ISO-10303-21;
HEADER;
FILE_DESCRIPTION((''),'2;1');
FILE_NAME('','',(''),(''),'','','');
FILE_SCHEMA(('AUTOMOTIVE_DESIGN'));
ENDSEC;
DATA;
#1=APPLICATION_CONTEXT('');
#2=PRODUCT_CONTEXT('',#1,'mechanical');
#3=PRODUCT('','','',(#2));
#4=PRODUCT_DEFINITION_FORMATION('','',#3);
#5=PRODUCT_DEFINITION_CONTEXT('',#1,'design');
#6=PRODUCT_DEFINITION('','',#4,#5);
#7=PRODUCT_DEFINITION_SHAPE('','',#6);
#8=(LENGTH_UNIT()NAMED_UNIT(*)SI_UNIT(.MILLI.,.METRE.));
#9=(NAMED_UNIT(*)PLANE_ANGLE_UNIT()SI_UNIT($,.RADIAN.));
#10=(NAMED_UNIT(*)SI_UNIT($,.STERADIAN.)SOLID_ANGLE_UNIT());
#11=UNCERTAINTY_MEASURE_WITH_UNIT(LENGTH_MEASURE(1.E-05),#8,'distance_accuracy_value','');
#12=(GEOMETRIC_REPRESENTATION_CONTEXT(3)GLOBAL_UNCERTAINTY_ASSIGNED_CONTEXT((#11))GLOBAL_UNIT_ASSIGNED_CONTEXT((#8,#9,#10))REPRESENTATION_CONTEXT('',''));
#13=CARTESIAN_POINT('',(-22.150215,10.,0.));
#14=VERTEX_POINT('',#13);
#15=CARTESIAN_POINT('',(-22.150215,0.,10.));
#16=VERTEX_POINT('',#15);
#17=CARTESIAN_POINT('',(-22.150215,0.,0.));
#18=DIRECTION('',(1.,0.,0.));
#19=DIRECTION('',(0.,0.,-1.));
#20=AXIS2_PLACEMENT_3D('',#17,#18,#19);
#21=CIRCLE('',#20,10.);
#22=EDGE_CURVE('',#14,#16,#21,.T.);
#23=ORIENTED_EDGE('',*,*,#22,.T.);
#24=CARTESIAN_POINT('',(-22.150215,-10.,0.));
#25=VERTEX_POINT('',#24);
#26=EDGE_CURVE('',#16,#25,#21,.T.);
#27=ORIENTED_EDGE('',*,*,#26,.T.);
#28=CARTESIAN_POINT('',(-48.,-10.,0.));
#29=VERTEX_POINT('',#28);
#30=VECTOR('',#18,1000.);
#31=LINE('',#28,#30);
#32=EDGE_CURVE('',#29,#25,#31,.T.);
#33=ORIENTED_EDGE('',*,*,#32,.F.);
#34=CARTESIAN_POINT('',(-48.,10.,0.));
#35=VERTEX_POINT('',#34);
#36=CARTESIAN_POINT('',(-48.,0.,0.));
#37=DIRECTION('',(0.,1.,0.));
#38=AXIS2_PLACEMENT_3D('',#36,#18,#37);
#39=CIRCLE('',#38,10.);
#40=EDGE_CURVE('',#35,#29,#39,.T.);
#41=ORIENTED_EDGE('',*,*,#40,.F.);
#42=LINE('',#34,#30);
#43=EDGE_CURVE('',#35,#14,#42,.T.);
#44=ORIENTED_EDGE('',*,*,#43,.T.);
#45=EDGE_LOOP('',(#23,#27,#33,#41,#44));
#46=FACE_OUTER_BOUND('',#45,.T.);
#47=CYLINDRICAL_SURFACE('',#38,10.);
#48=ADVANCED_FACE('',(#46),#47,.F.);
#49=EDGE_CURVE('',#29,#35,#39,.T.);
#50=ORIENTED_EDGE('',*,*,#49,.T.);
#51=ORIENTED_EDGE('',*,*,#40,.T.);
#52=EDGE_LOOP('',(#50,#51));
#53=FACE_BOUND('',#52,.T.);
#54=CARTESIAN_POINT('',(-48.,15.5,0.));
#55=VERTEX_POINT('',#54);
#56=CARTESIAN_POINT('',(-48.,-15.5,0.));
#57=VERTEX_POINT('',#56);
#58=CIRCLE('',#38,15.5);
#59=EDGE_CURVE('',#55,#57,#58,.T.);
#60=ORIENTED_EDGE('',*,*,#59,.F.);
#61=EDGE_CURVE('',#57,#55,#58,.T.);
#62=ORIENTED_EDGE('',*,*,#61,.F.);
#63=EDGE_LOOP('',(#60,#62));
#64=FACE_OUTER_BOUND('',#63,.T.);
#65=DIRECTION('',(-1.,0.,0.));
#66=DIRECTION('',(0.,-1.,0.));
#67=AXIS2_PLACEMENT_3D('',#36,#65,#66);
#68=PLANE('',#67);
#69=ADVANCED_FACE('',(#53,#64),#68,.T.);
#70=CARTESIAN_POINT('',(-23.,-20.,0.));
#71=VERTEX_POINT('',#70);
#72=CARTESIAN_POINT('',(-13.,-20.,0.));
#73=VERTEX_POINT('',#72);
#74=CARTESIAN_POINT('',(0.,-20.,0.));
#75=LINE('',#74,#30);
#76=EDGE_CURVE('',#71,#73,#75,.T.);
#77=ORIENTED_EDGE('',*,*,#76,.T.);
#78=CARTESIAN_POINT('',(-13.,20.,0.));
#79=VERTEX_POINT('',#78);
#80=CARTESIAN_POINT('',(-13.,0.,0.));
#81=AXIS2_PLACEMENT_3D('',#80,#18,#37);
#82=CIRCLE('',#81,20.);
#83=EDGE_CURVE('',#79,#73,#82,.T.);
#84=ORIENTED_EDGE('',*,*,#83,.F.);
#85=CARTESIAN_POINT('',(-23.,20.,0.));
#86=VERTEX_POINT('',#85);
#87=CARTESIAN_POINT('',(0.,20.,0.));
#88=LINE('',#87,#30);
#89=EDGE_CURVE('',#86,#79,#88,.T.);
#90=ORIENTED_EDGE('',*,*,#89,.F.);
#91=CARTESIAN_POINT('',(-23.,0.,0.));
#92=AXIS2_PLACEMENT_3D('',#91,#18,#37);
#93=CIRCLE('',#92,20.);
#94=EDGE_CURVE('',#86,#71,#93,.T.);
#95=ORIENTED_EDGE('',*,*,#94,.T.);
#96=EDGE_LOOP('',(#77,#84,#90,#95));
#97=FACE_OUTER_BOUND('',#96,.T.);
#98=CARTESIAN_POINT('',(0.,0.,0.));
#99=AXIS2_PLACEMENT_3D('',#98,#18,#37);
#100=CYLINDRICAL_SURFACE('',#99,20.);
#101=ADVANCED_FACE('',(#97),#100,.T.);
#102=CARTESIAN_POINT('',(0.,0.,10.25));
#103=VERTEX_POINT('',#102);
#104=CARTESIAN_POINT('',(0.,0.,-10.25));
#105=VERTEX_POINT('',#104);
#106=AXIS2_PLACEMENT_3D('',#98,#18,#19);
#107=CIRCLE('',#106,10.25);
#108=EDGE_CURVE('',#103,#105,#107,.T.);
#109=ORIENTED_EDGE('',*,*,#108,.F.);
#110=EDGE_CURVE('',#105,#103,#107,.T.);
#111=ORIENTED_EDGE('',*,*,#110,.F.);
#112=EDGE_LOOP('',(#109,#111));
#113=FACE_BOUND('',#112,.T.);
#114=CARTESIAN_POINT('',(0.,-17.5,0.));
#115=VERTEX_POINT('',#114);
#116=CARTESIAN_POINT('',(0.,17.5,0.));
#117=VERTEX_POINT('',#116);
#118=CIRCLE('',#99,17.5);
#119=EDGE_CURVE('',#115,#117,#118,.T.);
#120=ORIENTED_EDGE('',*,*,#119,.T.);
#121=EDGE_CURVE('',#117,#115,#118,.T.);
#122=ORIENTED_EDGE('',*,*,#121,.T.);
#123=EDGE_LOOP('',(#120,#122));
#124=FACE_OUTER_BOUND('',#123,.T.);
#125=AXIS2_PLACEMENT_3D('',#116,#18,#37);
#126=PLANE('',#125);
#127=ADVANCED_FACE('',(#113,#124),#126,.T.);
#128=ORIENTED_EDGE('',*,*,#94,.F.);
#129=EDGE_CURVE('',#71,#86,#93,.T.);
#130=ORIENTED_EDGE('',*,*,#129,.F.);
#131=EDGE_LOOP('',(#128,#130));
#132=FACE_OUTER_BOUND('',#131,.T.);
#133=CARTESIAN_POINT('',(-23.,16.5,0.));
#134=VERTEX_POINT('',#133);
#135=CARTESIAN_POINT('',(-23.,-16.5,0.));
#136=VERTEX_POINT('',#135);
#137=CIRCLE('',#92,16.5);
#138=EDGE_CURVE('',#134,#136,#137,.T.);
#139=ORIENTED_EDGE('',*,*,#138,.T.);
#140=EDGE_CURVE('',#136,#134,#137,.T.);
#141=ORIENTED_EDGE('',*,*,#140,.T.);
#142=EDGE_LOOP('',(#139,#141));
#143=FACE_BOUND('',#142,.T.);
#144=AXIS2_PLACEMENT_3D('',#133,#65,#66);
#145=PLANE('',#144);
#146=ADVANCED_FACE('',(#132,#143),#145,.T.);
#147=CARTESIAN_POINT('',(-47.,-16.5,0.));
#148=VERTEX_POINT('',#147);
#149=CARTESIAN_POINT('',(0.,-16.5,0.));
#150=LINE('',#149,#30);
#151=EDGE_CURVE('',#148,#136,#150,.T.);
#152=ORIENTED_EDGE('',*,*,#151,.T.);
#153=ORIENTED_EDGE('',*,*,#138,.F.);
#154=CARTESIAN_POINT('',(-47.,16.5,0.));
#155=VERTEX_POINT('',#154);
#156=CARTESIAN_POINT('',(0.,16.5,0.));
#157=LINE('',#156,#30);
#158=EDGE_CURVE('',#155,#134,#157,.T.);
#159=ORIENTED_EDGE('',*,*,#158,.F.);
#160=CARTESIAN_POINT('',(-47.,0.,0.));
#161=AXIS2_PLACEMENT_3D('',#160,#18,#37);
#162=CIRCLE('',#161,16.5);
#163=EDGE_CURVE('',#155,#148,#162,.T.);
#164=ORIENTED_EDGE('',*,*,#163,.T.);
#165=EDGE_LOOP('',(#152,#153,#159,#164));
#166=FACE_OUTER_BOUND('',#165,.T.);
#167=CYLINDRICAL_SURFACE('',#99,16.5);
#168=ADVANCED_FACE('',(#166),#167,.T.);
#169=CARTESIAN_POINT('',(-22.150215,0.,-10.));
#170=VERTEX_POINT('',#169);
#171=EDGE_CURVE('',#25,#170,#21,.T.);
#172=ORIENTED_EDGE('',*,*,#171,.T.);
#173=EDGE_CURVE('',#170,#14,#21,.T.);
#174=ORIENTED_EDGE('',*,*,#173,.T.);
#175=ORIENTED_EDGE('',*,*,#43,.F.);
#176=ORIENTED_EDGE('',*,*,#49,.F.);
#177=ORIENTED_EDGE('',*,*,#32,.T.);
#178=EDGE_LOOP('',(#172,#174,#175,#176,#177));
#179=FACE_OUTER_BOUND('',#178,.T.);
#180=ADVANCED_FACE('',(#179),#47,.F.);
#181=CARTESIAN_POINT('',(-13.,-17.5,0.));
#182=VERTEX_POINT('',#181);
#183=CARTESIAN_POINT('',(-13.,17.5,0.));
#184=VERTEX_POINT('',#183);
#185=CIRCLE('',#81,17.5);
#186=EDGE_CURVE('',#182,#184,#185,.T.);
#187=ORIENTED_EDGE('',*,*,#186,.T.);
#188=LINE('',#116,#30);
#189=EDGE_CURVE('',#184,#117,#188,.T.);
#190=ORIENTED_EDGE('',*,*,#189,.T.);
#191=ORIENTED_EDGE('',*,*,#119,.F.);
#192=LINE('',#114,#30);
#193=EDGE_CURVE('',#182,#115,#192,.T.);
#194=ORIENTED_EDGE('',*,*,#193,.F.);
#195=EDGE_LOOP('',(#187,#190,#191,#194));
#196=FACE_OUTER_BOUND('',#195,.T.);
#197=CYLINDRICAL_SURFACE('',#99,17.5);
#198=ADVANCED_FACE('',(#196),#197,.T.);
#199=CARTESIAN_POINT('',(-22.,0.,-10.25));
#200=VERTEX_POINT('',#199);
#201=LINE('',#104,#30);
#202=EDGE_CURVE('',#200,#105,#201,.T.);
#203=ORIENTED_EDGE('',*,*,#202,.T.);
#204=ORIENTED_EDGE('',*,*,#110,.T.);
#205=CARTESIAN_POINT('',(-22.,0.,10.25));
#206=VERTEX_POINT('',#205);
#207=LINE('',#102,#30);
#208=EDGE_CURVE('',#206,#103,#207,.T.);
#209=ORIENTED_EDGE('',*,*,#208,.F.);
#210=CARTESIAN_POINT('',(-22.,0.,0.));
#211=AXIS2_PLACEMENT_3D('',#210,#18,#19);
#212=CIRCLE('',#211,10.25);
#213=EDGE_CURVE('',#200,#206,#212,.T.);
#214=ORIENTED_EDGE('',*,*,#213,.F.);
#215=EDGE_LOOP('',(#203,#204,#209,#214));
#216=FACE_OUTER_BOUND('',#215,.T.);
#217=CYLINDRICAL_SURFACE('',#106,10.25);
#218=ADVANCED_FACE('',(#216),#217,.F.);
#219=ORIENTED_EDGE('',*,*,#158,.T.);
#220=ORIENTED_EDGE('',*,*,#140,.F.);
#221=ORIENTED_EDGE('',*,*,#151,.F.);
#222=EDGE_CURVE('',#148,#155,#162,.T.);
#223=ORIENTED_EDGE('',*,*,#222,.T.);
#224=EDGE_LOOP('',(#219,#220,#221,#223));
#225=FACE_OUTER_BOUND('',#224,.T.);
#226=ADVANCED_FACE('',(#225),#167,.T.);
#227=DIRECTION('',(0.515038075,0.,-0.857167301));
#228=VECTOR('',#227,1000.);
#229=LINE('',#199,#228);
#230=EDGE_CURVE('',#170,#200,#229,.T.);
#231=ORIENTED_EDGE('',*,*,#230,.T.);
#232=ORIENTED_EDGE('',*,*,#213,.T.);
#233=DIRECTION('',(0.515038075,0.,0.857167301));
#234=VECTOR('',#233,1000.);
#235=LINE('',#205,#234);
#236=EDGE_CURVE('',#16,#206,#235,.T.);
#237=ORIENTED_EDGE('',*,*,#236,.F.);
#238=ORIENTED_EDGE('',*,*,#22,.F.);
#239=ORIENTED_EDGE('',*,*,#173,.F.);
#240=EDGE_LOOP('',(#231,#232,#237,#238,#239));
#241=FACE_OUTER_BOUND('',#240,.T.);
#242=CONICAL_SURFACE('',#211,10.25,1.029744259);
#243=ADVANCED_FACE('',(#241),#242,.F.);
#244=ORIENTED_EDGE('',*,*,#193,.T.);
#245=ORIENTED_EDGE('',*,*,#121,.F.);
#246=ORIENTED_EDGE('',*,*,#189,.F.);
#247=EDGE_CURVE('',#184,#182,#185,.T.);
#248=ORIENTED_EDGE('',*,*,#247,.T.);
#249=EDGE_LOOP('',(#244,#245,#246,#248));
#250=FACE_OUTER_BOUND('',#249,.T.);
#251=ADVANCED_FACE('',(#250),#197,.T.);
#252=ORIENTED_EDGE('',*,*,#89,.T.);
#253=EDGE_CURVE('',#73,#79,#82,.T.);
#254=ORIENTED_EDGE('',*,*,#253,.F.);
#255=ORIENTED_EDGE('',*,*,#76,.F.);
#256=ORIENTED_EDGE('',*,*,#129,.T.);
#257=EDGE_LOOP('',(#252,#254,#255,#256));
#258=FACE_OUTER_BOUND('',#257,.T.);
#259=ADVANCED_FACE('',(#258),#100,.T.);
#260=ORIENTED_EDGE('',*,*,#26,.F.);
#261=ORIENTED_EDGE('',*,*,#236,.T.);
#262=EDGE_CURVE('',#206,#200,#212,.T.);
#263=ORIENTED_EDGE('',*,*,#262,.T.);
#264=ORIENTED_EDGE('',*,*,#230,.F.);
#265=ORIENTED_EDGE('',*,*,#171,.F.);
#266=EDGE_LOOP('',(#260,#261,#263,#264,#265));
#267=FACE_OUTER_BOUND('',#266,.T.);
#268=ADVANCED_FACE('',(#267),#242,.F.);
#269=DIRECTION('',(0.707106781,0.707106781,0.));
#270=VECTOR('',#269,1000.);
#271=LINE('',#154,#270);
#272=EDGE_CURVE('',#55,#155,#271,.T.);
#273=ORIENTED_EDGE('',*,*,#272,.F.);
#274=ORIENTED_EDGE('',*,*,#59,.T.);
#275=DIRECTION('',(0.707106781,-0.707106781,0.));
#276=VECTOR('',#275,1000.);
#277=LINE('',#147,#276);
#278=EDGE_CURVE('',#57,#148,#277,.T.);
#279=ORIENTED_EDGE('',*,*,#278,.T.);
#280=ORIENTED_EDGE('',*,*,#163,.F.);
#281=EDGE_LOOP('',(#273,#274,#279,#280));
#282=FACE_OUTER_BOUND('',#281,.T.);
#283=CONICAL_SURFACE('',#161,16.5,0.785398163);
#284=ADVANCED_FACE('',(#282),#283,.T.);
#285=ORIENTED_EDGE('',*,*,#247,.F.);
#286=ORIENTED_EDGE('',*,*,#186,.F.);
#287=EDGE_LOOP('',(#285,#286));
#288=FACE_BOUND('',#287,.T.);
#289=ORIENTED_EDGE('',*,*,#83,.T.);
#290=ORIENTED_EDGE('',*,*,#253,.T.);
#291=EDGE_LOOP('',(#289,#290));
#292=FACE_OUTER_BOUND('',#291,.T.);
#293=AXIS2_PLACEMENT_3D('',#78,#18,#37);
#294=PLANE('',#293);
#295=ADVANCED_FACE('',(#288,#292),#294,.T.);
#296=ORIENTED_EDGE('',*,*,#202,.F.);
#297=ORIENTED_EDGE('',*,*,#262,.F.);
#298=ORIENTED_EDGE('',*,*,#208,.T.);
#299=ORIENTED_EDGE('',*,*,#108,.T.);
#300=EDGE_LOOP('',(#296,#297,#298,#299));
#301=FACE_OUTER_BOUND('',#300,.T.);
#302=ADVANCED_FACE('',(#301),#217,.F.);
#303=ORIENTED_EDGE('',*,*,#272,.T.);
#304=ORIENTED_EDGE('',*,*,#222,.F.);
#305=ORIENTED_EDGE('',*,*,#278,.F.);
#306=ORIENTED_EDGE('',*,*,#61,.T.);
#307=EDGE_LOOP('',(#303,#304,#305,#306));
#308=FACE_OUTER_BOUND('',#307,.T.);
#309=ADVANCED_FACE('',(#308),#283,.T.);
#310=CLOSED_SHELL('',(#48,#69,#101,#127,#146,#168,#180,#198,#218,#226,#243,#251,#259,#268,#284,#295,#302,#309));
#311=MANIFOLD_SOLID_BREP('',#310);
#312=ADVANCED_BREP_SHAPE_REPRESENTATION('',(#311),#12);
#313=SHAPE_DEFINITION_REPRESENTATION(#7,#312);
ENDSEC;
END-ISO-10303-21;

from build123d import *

# Parameters (mm, degrees)
SKETCH2_R                  = 10
CUT_EXTRUDE1_DEPTH         = 56.713553109
M22X1_5_TAPPED_HOLE2_D     = 20.5
M22X1_5_TAPPED_HOLE2_DEPTH = 22
M22X1_5_TAPPED_HOLE2_TIP   = 6.158821345


with BuildPart() as part:
    # Sketch1 → Revolve1 (revolve)
    with BuildSketch(Plane.XY):
        Polygon((-48, 0), (-48, 15.5), (-47, 16.5), (-23, 16.5), (-23, 20), (-13, 20), (-13, 17.5), (0, 17.5), (0, 0), align=None)
    revolve(axis=Axis((0, 0, 0), (-1, 0, 0)))

    # Sketch2 → Cut-Extrude1 (cut, through all)
    with BuildSketch(Plane(origin=(0, 0, 0), x_dir=(0, 0, -1), z_dir=(1, 0, 0))):
        with Locations(Location((0, 0, 0), (0, 0, 90))):
            Circle(SKETCH2_R)
    extrude(amount=-CUT_EXTRUDE1_DEPTH, mode=Mode.SUBTRACT)

    # M22x1.5 Tapped Hole2
    with Locations(Plane(origin=(0, 0, 0), x_dir=(0, 0, -1), z_dir=(1, 0, 0))):
        with Locations((0, 0)):
            Hole(M22X1_5_TAPPED_HOLE2_D / 2, depth=M22X1_5_TAPPED_HOLE2_DEPTH)
            with Locations((0, 0, -(M22X1_5_TAPPED_HOLE2_DEPTH + M22X1_5_TAPPED_HOLE2_TIP / 2))):  # 118° drill point
                Cone(0, M22X1_5_TAPPED_HOLE2_D / 2, M22X1_5_TAPPED_HOLE2_TIP, mode=Mode.SUBTRACT)


solid = part.part
